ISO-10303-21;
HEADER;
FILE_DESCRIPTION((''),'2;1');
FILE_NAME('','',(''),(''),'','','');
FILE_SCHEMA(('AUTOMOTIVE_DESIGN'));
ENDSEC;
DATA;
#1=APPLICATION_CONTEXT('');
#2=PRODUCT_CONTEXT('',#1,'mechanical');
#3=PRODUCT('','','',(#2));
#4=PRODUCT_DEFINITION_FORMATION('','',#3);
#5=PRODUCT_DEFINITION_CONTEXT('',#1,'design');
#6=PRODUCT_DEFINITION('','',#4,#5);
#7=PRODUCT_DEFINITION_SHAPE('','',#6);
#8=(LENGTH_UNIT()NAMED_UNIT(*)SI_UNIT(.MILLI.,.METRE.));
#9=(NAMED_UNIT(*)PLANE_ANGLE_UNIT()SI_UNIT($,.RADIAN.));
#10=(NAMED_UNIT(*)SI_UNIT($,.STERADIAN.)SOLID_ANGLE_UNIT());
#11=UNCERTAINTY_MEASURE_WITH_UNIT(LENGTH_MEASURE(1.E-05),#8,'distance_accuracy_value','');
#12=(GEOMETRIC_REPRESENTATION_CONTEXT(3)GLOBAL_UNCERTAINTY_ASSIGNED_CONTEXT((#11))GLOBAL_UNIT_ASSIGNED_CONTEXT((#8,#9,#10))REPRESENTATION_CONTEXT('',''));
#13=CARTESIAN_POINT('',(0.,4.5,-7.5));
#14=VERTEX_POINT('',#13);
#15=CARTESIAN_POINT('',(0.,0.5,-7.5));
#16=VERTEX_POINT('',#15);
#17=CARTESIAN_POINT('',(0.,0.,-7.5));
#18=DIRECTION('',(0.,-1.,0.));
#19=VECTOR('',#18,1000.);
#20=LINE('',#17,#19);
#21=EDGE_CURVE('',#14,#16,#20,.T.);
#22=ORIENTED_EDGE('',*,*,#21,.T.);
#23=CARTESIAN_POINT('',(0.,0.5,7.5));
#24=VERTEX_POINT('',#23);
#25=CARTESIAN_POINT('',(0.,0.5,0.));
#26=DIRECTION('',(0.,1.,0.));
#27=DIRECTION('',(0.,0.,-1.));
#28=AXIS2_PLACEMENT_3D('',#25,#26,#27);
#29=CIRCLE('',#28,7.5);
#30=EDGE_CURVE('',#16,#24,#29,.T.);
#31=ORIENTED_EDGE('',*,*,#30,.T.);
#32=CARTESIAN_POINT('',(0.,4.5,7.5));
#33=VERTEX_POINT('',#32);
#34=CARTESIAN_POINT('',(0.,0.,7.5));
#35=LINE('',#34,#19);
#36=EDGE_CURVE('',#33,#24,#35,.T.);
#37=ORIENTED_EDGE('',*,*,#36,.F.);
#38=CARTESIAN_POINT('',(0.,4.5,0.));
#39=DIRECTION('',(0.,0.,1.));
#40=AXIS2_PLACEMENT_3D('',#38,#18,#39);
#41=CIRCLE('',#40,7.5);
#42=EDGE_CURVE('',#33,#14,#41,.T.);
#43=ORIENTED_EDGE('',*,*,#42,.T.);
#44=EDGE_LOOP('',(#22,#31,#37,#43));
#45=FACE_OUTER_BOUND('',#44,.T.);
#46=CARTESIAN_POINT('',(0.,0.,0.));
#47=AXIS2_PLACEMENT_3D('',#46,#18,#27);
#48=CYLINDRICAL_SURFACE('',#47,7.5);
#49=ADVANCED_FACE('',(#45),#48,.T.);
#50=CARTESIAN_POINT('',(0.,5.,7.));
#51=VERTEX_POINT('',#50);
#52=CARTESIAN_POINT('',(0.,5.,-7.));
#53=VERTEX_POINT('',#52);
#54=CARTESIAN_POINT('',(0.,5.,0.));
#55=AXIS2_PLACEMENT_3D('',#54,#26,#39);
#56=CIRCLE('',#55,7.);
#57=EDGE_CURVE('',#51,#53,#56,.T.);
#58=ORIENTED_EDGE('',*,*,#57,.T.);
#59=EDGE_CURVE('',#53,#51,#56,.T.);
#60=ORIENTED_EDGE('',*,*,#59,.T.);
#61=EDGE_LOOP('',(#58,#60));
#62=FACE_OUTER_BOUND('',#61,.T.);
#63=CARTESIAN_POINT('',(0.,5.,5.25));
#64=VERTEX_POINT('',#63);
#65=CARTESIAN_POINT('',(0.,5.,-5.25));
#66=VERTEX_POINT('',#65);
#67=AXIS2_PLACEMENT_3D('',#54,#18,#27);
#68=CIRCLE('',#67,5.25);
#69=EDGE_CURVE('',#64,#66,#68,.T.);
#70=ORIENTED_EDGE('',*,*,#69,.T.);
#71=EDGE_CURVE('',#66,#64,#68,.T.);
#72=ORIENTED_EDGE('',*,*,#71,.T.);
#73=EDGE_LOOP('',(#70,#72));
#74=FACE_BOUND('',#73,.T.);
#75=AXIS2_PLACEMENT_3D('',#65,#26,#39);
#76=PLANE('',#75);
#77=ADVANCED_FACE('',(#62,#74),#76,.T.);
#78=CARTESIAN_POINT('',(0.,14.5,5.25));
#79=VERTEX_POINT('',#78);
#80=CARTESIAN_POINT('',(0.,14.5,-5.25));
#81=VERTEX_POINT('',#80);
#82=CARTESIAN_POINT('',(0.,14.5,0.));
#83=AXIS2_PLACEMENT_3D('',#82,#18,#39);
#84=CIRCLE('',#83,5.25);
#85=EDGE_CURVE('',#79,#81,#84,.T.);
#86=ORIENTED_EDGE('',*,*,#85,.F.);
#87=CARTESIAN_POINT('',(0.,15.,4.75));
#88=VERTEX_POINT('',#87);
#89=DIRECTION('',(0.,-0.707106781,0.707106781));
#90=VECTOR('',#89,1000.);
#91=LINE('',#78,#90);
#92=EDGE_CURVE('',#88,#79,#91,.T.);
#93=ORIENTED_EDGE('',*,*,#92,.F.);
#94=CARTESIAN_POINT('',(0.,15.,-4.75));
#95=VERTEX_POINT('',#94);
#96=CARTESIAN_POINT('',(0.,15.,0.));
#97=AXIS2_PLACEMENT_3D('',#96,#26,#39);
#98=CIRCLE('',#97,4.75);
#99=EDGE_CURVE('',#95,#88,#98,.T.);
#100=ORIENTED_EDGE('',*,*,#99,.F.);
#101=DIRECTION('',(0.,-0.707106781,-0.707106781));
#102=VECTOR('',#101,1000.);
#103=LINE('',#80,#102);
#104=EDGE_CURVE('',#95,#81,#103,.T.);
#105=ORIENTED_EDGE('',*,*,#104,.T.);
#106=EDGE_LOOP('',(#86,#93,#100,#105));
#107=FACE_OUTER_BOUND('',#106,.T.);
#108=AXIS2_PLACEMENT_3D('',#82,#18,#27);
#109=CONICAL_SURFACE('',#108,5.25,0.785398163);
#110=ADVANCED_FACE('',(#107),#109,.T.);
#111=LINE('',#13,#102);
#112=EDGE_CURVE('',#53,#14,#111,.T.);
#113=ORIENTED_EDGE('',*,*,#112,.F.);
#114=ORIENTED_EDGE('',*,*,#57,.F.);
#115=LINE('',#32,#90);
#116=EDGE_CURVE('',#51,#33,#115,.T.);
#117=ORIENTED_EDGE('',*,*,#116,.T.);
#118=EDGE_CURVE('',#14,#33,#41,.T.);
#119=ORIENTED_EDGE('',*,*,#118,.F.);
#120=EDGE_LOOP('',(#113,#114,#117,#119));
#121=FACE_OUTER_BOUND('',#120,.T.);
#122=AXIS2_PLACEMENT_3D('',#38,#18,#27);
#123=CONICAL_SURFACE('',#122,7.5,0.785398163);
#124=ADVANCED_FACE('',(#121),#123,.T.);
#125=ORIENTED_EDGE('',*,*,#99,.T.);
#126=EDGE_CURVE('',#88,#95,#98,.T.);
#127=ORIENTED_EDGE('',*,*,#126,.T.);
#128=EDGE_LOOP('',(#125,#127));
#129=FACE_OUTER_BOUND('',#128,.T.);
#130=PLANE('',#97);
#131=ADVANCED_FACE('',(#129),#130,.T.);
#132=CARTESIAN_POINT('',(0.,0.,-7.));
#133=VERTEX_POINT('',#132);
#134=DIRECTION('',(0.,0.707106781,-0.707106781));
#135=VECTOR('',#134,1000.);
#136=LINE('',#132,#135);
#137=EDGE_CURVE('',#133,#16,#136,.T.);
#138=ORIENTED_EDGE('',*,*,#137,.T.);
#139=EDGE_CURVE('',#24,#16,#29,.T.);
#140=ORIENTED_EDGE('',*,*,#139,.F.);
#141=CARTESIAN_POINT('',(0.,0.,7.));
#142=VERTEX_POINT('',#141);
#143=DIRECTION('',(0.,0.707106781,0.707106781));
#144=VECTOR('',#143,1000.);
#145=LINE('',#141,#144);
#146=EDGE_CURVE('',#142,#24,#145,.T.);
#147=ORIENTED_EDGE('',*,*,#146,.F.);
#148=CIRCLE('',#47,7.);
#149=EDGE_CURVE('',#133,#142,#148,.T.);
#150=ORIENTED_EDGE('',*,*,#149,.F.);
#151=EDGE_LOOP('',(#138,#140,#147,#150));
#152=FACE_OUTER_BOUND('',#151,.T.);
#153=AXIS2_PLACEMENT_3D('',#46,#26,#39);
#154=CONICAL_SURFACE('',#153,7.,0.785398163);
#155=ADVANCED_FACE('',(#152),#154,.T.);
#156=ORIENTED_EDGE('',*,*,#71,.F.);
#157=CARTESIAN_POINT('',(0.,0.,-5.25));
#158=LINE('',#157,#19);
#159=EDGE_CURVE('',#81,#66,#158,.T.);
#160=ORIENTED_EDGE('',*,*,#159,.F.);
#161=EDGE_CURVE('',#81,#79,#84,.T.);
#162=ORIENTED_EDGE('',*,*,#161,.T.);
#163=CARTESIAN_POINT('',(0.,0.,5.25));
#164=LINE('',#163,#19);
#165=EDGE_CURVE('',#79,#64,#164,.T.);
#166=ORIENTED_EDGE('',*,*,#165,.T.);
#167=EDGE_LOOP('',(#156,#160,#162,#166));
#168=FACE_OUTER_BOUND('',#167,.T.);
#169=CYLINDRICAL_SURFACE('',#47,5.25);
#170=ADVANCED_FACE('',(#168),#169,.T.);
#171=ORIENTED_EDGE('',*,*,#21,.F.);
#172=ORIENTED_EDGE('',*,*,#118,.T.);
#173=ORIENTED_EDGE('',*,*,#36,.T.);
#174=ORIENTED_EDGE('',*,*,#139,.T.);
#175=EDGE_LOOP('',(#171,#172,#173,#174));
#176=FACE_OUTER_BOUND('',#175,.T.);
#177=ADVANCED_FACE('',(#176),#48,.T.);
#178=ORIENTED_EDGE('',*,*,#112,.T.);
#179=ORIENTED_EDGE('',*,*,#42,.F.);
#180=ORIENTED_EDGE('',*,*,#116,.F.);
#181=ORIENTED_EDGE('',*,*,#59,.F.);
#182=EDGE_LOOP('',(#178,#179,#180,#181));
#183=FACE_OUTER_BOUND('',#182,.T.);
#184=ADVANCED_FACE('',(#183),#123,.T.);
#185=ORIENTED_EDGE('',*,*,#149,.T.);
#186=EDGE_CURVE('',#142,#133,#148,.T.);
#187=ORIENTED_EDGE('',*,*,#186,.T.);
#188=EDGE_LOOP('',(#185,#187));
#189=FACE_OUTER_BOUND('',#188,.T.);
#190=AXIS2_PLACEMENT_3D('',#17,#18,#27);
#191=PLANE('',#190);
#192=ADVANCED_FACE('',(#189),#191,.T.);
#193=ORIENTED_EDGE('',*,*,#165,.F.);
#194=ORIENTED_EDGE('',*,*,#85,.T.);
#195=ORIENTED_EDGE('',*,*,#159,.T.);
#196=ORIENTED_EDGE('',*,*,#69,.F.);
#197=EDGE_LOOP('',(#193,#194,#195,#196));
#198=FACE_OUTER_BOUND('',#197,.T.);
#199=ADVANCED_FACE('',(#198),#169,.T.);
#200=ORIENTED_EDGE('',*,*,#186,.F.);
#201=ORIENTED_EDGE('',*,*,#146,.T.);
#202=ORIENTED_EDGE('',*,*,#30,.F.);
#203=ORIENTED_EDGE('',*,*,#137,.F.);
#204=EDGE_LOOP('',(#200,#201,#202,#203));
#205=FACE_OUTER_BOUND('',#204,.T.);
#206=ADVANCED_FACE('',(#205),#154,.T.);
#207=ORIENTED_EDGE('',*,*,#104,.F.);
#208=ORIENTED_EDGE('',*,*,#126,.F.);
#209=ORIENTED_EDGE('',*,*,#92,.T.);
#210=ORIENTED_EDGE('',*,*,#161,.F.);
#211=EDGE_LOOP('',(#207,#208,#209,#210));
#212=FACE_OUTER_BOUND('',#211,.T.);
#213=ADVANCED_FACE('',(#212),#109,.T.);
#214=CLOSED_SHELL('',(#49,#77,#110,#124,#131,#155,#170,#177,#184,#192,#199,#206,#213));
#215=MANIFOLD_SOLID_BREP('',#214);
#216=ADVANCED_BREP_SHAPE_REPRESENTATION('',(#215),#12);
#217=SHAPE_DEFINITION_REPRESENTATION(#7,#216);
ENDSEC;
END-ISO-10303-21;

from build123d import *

# Parameters (mm, degrees)
CHAMFER1_SIZE = 0.5


with BuildPart() as part:
    # Sketch1 → Revolve1 (revolve)
    with BuildSketch(Plane(origin=(0, 0, 0), x_dir=(0, 0, -1), z_dir=(1, 0, 0))):
        Polygon((0, 15), (5.25, 15), (5.25, 5), (7.5, 5), (7.5, 0), (0, 0), align=None)
    revolve(axis=Axis((0, 0, 0), (0, 1, 0)))

    # Chamfer1
    chamfer1_edges = [part.edges().sort_by_distance(p)[0] for p in [
        (0, 0, 7.5),
        (0, 5, 7.5),
        (0, 15, 5.25),
    ]]
    chamfer(chamfer1_edges, length=CHAMFER1_SIZE)


solid = part.part
